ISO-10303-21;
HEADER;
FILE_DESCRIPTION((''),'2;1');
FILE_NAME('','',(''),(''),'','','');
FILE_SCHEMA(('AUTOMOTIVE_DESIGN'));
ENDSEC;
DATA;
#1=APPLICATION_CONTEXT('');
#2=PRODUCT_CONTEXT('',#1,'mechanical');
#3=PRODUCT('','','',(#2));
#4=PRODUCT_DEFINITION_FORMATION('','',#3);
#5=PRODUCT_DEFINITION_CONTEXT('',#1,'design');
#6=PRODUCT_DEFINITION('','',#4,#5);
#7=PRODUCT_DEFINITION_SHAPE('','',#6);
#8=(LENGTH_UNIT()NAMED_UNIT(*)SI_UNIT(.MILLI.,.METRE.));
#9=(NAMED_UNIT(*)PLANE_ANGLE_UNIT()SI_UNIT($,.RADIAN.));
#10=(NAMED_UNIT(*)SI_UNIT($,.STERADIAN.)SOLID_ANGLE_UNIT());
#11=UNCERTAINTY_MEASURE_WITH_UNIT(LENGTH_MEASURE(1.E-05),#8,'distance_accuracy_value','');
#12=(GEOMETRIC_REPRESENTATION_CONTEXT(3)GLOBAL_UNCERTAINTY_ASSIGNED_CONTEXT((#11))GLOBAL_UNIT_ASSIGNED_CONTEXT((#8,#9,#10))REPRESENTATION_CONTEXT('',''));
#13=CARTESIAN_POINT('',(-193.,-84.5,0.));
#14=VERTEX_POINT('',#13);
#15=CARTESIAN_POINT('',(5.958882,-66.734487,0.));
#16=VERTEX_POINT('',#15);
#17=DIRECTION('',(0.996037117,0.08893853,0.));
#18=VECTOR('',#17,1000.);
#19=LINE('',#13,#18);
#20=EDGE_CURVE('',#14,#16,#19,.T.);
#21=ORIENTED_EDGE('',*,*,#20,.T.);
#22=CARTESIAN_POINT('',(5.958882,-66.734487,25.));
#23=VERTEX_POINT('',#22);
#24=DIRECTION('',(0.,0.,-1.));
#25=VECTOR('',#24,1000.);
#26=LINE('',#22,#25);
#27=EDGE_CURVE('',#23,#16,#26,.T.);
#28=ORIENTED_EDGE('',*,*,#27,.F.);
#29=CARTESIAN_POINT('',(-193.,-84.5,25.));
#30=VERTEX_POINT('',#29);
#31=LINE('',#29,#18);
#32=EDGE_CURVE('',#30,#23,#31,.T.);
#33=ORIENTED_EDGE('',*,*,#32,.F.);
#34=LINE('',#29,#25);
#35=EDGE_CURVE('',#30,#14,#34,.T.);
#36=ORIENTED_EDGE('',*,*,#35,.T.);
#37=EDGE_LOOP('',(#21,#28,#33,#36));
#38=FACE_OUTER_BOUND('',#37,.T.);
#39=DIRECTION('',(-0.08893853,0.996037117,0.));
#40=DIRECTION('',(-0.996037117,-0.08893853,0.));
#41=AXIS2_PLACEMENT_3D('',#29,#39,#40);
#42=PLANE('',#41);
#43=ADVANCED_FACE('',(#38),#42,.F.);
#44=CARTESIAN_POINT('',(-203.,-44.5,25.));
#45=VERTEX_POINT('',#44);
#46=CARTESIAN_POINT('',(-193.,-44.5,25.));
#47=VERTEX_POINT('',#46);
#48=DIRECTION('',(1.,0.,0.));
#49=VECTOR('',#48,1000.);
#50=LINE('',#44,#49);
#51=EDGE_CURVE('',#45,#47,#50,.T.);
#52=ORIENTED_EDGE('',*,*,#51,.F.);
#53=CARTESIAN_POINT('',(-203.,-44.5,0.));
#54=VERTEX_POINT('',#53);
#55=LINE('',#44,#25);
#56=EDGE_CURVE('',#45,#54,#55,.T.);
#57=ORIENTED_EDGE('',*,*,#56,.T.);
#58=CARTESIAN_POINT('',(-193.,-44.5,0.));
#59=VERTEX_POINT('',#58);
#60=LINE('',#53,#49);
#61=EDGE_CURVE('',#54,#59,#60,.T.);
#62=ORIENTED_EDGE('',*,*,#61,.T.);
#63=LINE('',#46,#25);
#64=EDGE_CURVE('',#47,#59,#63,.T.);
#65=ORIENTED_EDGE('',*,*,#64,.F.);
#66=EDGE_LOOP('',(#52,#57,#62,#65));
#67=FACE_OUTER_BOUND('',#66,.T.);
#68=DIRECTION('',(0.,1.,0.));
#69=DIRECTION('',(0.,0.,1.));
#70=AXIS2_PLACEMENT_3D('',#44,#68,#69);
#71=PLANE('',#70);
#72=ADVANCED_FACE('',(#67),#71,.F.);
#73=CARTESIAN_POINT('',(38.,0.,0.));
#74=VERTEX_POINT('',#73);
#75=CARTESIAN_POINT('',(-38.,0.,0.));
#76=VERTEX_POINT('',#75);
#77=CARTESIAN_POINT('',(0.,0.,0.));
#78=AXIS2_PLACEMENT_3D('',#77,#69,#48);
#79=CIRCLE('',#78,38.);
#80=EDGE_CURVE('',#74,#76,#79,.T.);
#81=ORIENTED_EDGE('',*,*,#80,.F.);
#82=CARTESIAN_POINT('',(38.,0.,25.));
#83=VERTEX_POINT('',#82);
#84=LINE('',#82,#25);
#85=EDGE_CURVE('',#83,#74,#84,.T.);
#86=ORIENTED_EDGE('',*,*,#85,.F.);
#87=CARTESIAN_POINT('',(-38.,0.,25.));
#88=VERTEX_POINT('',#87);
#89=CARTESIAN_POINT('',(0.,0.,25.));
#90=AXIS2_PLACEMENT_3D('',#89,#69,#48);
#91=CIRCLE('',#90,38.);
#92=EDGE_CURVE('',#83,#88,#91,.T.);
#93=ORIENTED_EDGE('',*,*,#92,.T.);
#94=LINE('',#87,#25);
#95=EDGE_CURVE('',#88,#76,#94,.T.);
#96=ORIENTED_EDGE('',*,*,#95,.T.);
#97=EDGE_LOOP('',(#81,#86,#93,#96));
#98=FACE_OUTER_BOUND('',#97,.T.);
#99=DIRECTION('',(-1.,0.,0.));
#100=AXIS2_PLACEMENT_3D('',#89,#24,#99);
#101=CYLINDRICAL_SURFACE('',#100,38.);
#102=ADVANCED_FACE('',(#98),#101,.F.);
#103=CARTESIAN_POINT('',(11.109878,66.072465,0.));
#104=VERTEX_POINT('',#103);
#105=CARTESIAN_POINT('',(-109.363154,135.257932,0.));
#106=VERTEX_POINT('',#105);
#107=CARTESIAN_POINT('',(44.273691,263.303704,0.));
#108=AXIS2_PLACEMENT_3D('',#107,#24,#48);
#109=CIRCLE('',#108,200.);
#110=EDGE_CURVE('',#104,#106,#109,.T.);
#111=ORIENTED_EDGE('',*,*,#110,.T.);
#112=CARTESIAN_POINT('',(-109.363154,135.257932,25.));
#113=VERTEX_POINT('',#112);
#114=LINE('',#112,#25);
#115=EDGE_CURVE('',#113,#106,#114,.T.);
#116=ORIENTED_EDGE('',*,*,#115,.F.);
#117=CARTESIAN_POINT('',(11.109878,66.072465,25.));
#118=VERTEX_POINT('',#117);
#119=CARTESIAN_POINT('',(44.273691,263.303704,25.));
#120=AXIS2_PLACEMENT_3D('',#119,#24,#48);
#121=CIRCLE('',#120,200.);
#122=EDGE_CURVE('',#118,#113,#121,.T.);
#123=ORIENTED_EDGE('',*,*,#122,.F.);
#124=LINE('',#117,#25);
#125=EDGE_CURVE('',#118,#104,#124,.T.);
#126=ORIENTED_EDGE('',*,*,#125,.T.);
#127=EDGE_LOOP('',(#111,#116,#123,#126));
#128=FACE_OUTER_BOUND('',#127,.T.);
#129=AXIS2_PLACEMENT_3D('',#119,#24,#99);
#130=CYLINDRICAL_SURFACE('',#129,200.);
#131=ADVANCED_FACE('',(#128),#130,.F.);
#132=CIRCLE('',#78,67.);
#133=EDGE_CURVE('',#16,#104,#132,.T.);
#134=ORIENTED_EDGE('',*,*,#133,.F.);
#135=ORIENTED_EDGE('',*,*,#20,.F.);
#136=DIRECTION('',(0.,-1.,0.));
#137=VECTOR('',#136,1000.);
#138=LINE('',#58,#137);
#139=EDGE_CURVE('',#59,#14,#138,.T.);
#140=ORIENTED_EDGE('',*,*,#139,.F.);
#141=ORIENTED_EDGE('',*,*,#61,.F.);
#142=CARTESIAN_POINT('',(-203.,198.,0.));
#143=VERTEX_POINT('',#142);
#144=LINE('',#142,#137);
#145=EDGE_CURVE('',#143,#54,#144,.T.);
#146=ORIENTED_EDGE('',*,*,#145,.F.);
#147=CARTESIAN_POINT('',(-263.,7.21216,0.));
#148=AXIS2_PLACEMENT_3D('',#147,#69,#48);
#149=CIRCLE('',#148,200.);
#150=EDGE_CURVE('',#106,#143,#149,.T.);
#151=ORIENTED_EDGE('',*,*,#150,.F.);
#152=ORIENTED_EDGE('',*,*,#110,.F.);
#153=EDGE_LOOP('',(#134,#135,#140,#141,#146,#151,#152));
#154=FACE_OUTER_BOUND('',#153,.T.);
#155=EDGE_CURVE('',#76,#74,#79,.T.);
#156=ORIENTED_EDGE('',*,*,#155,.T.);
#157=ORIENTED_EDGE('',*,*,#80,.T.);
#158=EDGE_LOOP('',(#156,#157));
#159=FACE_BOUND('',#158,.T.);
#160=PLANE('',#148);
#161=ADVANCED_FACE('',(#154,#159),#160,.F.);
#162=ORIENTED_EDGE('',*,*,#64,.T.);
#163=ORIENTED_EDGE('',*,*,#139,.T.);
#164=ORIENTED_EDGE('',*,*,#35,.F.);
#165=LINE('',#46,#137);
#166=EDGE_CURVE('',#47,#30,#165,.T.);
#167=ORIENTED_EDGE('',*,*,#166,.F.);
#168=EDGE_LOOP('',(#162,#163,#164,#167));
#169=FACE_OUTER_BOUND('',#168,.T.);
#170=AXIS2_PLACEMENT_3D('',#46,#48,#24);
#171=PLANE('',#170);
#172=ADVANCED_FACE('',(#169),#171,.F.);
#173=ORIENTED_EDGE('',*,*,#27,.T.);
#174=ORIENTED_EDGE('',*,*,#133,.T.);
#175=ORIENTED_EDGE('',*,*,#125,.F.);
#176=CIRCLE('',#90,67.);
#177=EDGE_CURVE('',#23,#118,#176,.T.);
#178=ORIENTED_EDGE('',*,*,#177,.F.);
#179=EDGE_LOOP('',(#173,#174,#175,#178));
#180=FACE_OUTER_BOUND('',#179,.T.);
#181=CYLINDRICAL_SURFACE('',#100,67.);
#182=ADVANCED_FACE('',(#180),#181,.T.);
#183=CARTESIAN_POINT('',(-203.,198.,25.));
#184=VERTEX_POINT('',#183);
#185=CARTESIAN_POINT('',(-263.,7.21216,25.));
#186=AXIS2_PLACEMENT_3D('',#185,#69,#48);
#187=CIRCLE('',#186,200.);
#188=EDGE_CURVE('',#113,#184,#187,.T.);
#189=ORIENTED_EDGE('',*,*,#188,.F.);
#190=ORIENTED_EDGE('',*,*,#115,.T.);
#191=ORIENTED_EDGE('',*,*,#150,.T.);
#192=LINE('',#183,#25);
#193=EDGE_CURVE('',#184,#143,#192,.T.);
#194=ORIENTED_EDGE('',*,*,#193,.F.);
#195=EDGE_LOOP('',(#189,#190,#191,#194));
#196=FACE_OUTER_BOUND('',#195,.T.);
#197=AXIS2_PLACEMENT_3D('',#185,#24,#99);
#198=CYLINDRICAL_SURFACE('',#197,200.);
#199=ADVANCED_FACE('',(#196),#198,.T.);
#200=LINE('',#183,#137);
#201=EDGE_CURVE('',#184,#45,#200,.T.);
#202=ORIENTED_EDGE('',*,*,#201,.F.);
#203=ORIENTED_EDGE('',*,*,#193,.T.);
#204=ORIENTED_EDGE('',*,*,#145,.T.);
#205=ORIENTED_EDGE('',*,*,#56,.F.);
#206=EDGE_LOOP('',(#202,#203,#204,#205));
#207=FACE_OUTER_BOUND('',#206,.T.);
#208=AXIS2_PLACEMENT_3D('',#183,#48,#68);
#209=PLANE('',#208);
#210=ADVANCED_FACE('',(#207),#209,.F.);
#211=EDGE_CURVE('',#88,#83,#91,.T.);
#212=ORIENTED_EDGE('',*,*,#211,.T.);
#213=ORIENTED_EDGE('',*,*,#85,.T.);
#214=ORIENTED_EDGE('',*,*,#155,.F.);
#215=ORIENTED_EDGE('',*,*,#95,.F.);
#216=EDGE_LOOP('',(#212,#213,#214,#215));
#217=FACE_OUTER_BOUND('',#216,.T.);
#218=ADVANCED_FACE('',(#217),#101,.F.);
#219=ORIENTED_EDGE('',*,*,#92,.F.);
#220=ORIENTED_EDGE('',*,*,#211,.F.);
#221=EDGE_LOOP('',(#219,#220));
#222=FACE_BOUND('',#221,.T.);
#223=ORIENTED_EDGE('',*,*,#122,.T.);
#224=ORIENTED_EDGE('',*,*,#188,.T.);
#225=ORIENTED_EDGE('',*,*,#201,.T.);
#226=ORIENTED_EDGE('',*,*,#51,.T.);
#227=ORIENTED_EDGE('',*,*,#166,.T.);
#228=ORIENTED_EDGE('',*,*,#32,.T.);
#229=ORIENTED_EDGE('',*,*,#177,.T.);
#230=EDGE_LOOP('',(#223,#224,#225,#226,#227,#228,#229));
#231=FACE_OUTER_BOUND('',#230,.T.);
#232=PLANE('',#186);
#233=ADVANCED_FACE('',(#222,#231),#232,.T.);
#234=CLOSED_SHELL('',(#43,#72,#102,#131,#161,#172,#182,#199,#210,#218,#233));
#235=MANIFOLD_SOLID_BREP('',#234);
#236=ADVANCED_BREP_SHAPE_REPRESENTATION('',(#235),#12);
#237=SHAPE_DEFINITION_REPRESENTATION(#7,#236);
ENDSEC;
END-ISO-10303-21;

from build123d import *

# Parameters (mm, degrees)
SKETCH1_R           = 38
BOSS_EXTRUDE1_DEPTH = 25


with BuildPart() as part:
    # Sketch1 → Boss-Extrude1 (new body)
    with BuildSketch(Plane.XY):
        with BuildLine():
            Line((-203, 198), (-203, -44.5))
            Line((-203, -44.5), (-193, -44.5))
            Line((-193, -44.5), (-193, -84.5))
            Line((-193, -84.5), (5.958881534, -66.734486818))
            ThreePointArc((5.958881534, -66.734486818), (66.949661999, -2.596682146), (11.109877523, 66.072464926))
            ThreePointArc((11.109877523, 66.072464926), (-55.326905119, 89.868640022), (-109.363154487, 135.257931614))
            ThreePointArc((-109.363154487, 135.257931614), (-151.670232074, 173.361739233), (-203, 198))
        make_face()
        Circle(SKETCH1_R, mode=Mode.SUBTRACT)
    extrude(amount=BOSS_EXTRUDE1_DEPTH)


solid = part.part
